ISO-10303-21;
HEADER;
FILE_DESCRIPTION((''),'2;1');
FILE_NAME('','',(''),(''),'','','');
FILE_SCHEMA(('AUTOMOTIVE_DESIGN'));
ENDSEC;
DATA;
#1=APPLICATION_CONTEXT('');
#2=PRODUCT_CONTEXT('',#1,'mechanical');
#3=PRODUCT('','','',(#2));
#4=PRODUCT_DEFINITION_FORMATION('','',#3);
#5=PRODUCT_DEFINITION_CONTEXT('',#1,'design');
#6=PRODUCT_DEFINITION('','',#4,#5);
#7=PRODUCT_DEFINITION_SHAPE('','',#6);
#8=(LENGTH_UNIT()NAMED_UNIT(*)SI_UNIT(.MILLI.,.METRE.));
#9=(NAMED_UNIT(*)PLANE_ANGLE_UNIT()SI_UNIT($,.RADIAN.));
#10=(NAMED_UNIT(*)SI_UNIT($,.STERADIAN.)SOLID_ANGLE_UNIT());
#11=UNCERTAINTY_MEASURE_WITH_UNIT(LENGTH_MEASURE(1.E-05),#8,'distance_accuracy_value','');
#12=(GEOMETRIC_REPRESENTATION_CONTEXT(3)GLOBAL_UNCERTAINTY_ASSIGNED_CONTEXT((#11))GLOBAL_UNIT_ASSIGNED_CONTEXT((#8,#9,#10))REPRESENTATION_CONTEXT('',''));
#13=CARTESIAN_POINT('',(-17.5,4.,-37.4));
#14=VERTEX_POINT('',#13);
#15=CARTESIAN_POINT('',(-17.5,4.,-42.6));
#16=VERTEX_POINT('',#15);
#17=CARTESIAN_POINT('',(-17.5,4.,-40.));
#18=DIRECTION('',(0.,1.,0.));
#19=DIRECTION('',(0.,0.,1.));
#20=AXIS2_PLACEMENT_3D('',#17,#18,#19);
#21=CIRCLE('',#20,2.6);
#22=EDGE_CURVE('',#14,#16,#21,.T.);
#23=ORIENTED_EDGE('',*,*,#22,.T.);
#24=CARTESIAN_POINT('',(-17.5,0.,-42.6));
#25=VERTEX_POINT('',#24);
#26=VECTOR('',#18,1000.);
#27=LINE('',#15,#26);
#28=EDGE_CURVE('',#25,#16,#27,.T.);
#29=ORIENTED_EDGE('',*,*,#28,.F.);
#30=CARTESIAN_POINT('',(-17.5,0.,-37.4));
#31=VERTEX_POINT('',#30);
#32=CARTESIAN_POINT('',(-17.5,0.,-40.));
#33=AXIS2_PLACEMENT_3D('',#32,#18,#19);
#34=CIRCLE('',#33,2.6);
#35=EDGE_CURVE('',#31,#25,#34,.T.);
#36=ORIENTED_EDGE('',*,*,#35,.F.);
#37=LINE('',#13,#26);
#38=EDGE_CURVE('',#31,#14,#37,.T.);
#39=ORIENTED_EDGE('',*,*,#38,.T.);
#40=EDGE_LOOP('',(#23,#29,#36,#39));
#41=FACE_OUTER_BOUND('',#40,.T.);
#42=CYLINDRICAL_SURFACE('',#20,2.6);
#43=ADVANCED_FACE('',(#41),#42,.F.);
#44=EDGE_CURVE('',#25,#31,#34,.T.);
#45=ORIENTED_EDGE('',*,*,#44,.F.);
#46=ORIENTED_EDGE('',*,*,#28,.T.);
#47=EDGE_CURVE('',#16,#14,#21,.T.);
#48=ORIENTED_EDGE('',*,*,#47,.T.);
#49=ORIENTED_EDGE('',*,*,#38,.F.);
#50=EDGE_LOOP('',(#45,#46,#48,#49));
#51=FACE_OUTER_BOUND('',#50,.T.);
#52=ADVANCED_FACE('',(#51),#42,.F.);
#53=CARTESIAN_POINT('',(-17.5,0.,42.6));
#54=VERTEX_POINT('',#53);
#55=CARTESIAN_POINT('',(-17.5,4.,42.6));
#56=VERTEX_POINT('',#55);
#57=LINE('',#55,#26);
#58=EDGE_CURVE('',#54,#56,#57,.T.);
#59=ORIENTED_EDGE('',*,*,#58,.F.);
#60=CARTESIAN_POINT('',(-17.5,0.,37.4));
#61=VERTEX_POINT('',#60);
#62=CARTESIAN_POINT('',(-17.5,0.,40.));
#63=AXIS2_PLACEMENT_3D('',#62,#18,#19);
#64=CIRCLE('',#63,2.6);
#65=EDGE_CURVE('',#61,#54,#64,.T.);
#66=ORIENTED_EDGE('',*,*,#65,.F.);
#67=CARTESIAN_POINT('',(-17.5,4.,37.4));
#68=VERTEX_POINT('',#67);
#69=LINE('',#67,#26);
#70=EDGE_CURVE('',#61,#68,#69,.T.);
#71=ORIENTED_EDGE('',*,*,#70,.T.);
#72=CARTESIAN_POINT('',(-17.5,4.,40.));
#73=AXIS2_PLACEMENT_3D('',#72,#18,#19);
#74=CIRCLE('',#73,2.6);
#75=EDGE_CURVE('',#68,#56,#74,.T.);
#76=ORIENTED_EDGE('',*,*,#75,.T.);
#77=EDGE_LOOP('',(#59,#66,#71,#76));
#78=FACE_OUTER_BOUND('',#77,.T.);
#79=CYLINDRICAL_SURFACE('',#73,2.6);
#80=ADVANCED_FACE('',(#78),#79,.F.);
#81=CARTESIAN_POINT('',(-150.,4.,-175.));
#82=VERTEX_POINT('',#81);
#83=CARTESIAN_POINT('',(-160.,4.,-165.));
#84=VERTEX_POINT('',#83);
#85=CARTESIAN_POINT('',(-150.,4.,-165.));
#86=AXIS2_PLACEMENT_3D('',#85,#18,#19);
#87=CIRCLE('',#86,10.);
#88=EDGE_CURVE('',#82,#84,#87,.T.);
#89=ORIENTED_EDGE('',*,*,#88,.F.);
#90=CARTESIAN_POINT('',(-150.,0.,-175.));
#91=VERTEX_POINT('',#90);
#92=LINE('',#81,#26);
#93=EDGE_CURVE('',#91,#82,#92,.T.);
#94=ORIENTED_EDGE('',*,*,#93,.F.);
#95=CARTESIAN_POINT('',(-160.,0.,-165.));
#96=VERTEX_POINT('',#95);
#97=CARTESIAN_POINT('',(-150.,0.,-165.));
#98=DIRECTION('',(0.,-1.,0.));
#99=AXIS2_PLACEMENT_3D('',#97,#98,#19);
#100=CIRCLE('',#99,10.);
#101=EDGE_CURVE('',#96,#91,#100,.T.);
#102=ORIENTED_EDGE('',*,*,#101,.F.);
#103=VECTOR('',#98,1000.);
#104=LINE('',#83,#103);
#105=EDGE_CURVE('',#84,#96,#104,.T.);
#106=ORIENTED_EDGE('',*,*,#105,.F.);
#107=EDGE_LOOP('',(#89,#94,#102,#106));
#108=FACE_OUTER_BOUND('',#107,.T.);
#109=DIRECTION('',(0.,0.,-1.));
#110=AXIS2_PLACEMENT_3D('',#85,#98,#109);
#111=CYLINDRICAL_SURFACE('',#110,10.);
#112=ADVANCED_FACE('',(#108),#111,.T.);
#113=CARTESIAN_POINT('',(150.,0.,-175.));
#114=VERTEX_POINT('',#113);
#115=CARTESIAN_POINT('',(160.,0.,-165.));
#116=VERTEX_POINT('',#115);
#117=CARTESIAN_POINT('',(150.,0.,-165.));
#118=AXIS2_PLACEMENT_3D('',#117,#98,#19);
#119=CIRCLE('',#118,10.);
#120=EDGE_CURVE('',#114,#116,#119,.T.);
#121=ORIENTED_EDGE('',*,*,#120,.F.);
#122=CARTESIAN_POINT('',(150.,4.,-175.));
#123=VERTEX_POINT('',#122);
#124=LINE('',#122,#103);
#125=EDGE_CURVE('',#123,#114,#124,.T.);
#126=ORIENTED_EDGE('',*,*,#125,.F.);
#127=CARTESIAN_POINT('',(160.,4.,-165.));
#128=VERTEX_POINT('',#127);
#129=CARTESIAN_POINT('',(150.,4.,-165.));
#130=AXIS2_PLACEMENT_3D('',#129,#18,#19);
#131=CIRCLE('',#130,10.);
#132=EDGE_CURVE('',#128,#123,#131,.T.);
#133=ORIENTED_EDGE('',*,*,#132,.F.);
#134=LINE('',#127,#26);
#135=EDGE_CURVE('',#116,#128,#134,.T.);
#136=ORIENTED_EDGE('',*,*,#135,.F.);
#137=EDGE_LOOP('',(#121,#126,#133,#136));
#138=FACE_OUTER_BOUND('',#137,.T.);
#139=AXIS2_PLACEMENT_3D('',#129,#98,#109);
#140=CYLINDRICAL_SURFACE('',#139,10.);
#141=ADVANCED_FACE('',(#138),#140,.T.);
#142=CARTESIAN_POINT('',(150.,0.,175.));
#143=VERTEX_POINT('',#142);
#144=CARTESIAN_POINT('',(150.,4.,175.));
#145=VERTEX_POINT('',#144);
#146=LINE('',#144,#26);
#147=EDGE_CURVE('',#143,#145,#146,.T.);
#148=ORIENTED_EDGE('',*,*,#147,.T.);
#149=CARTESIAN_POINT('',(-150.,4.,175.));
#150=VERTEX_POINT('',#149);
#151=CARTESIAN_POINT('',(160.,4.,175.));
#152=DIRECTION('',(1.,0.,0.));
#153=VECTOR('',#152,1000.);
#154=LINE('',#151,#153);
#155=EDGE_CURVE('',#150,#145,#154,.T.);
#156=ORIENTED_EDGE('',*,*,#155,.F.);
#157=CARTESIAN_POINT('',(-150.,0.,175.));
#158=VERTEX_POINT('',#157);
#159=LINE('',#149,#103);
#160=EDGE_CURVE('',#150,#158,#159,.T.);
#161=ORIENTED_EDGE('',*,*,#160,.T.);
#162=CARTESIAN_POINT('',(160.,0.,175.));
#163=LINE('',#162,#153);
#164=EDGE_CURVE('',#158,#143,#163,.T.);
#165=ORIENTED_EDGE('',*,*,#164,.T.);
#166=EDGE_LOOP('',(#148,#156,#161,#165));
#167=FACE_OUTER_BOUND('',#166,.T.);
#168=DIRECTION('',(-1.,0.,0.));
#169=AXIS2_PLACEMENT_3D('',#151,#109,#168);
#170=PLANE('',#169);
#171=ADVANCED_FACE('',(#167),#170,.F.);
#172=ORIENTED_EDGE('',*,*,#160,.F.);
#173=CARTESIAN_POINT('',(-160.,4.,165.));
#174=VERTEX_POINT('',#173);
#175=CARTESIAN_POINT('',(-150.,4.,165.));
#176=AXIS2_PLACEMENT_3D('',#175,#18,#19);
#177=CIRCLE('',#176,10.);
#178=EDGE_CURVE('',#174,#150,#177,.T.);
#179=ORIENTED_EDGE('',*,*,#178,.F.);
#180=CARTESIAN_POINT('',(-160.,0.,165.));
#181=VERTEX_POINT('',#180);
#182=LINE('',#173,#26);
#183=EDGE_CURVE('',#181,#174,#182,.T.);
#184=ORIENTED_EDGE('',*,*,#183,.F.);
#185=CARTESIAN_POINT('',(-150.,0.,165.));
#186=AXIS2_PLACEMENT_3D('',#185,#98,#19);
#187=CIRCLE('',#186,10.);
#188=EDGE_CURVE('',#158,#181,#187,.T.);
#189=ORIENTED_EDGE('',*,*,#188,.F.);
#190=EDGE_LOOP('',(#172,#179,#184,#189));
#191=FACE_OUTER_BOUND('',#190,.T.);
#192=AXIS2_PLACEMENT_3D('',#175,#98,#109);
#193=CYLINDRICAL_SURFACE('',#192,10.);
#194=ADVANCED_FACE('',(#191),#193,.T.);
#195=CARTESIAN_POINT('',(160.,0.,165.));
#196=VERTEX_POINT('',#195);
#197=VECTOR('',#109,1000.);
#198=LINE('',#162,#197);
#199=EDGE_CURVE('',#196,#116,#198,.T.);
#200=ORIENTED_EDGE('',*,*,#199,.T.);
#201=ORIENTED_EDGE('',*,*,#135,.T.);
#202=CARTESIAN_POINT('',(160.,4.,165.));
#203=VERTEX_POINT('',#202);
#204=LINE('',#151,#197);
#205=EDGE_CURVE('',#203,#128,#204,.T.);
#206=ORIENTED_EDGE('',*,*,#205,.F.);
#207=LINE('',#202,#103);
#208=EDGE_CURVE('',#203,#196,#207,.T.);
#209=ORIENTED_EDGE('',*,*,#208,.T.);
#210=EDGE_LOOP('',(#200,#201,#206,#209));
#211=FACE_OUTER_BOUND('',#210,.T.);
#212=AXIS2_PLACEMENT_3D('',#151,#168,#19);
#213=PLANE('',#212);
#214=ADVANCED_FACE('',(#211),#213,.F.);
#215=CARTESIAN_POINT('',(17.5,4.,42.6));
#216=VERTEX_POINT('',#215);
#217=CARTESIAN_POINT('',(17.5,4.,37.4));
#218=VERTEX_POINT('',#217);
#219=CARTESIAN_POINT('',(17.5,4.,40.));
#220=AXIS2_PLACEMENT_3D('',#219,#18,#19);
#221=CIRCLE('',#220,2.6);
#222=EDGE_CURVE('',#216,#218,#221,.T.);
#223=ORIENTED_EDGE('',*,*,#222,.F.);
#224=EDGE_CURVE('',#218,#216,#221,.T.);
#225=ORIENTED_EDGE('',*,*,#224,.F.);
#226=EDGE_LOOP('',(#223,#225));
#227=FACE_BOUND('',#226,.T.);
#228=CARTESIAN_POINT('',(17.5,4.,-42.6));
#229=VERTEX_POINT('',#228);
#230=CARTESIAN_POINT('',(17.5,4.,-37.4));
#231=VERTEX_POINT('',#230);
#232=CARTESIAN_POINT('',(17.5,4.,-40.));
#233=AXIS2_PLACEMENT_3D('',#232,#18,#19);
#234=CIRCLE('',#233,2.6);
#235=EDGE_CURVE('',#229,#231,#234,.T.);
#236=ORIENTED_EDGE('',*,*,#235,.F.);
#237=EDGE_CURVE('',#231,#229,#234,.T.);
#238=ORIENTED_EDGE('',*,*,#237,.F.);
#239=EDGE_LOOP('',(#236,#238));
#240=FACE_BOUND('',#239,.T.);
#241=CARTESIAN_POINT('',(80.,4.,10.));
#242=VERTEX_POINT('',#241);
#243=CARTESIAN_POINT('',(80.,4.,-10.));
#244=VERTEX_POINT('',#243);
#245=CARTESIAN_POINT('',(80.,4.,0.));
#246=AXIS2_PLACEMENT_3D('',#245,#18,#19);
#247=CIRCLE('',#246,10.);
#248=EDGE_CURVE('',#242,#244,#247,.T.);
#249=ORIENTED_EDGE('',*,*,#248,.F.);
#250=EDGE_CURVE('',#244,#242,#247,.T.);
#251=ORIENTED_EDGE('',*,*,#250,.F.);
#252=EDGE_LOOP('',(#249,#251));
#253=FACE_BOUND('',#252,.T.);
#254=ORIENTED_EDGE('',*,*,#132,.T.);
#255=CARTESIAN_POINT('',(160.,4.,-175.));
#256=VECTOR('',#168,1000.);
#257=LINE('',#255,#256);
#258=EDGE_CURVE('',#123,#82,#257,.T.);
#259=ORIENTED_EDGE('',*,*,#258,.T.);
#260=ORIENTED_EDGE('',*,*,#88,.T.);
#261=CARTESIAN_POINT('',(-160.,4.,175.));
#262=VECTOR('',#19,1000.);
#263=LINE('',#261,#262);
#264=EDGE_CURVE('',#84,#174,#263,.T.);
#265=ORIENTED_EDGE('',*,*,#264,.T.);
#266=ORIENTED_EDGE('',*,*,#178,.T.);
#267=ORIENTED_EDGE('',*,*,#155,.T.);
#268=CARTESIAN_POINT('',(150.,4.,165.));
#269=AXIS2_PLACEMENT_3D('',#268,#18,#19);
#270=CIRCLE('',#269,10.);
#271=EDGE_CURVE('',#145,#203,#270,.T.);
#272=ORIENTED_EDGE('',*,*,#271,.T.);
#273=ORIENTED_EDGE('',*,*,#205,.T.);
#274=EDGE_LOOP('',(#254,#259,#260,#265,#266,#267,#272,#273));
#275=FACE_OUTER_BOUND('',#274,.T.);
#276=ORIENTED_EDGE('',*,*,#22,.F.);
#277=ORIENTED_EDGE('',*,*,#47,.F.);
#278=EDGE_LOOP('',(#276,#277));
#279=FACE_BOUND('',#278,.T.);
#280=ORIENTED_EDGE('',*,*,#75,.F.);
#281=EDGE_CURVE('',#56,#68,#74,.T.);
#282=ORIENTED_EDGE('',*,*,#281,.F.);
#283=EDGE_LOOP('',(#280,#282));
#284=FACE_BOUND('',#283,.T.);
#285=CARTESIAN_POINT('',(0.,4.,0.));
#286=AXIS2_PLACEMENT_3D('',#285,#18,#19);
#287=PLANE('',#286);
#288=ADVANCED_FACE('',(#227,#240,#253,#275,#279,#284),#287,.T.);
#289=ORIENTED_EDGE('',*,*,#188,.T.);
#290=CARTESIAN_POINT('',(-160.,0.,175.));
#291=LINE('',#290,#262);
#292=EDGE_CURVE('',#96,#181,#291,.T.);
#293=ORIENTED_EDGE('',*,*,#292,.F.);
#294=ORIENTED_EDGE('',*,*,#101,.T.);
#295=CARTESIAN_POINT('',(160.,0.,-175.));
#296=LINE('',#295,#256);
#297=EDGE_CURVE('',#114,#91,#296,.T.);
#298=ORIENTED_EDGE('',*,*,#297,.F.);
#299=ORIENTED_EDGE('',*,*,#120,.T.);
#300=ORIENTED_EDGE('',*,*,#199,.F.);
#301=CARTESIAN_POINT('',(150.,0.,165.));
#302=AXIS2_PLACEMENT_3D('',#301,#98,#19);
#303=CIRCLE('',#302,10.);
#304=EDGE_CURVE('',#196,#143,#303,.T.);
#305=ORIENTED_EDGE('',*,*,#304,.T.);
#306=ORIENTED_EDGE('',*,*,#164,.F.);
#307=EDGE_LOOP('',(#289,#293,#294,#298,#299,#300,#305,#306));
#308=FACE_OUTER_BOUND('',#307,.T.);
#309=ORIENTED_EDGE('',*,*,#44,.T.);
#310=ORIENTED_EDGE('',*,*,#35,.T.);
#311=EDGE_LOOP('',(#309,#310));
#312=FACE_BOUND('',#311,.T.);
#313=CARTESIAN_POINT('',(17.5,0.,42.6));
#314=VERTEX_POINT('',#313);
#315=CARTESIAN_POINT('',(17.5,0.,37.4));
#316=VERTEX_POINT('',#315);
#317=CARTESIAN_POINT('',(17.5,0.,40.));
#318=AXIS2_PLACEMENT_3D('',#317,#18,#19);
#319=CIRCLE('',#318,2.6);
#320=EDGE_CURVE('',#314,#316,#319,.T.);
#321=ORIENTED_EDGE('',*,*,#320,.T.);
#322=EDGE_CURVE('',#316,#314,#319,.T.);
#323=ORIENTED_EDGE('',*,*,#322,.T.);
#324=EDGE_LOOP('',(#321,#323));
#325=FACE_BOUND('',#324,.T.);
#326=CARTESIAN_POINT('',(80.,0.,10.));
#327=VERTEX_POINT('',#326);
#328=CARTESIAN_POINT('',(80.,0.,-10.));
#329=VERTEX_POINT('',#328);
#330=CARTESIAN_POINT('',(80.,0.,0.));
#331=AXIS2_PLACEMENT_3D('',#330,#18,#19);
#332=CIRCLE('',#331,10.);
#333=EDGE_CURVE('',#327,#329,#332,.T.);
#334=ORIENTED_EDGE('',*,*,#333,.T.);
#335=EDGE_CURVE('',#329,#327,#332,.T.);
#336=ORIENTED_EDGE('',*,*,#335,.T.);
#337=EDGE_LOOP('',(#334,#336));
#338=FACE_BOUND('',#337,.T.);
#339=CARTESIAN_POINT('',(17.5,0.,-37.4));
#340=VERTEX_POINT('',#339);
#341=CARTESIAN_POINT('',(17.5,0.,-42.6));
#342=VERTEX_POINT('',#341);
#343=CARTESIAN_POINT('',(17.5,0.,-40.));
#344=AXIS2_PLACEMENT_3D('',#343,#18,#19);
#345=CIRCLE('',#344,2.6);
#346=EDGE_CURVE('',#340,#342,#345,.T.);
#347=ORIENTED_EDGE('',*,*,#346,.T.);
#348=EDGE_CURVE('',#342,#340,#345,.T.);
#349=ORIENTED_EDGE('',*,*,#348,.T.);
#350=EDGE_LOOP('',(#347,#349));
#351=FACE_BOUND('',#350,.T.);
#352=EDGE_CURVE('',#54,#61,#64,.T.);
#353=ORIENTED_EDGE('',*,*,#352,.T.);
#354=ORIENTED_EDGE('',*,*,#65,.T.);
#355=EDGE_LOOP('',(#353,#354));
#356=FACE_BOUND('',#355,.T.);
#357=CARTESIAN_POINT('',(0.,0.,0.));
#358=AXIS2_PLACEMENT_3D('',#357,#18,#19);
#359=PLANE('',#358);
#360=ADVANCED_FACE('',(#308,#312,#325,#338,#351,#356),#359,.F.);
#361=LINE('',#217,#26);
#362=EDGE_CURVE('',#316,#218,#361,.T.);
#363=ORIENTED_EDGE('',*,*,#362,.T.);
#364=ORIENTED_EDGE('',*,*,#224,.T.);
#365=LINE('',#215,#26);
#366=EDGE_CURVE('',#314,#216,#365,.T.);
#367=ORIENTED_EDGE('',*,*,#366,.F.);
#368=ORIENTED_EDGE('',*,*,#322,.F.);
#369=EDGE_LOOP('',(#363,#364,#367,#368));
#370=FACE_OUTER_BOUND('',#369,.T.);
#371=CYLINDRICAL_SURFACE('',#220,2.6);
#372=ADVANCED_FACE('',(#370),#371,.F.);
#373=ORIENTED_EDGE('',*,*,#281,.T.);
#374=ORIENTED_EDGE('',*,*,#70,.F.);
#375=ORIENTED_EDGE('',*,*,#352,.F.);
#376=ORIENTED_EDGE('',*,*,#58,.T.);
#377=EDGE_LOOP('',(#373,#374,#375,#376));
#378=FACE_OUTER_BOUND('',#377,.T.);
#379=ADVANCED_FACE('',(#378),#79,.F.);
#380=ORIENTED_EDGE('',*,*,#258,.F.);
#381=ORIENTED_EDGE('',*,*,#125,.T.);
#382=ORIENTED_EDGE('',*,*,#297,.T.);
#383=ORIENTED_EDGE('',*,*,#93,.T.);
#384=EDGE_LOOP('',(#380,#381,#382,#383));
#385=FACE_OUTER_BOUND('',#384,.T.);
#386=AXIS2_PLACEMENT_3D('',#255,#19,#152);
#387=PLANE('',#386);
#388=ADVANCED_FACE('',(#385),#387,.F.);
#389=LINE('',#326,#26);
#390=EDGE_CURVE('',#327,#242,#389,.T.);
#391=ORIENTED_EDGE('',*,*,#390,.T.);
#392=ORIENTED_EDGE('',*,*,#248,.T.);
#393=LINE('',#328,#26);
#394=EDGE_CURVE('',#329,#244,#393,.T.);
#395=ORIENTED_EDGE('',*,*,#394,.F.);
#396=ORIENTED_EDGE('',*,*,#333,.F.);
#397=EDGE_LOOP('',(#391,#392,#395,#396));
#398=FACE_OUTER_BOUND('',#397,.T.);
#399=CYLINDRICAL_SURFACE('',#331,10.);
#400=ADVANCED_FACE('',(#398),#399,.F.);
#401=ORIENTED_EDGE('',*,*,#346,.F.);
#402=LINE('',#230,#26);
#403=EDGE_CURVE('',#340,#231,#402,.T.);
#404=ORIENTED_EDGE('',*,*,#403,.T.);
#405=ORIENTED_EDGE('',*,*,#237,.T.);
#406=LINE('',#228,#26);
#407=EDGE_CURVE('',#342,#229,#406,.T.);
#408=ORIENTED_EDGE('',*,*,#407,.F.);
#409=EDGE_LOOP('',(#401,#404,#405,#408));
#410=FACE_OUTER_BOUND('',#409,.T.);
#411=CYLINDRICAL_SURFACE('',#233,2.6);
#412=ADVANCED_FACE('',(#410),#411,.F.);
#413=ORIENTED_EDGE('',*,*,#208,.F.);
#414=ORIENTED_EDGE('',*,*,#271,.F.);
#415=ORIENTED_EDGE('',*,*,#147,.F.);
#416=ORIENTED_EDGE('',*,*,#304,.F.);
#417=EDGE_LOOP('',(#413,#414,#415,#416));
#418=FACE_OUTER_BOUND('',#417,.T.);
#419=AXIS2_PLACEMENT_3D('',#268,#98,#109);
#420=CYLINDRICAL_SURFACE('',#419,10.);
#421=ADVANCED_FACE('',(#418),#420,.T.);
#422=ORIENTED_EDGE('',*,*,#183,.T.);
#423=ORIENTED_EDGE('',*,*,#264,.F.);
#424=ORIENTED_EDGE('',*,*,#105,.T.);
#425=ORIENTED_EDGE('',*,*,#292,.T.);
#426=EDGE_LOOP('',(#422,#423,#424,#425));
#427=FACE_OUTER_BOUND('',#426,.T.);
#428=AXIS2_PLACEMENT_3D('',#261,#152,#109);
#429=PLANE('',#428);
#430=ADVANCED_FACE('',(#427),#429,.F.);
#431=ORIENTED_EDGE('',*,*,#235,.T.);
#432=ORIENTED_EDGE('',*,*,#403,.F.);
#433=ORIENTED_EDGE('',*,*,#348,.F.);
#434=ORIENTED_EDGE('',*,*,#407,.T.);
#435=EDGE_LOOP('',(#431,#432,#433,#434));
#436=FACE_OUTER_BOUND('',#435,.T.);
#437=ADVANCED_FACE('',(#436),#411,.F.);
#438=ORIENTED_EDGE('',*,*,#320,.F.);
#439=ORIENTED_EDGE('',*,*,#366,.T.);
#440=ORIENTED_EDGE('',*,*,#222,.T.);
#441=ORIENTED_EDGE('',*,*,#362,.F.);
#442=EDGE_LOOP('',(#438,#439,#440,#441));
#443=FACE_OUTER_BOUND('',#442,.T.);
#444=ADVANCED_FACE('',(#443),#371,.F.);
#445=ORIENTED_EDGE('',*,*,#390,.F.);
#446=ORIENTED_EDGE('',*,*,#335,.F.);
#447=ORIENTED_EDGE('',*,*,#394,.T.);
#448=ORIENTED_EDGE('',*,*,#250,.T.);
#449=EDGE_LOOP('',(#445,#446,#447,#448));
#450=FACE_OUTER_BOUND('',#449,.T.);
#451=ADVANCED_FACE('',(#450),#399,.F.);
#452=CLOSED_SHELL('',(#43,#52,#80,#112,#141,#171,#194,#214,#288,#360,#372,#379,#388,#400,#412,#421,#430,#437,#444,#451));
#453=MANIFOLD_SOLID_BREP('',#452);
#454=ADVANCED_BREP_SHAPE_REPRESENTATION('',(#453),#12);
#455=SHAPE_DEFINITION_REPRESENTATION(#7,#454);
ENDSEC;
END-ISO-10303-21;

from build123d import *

# Parameters (mm, degrees)
SKETCH1_W                      = 320
SKETCH1_H                      = 350
BOSS_EXTRUDE1_DEPTH            = 4
F_5_2_5_2_DIAMETER_HOLE1_D     = 5.2
F_5_2_5_2_DIAMETER_HOLE1_DEPTH = 10.1
F_5_2_5_2_DIAMETER_HOLE1_TIP   = 1.562237609
FILLET1_R                      = 10
SKETCH4_R                      = 10
CUT_EXTRUDE1_DEPTH             = 238.151850088


with BuildPart() as part:
    # Sketch1 → Boss-Extrude1 (new body)
    with BuildSketch(Plane(origin=(0, 0, 0), x_dir=(1, 0, 0), z_dir=(0, 1, 0))):
        Rectangle(SKETCH1_W, SKETCH1_H)
    extrude(amount=BOSS_EXTRUDE1_DEPTH)

    # Ø5.2 (5.2) Diameter Hole1
    with Locations(Plane(origin=(0, 4, 0), x_dir=(1, 0, 0), z_dir=(0, 1, 0))):
        with Locations((-17.5, 40), (17.5, -40), (-17.5, -40), (17.5, 40)):
            Hole(F_5_2_5_2_DIAMETER_HOLE1_D / 2, depth=F_5_2_5_2_DIAMETER_HOLE1_DEPTH)
            with Locations((0, 0, -(F_5_2_5_2_DIAMETER_HOLE1_DEPTH + F_5_2_5_2_DIAMETER_HOLE1_TIP / 2))):  # 118° drill point
                Cone(0, F_5_2_5_2_DIAMETER_HOLE1_D / 2, F_5_2_5_2_DIAMETER_HOLE1_TIP, mode=Mode.SUBTRACT)

    # Fillet1
    fillet1_edges = [part.edges().sort_by_distance(p)[0] for p in [
        (-160, 2, -175),
        (160, 2, -175),
        (160, 2, 175),
        (-160, 2, 175),
    ]]
    fillet(fillet1_edges, radius=FILLET1_R)

    # Sketch4 → Cut-Extrude1 (cut, through all)
    with BuildSketch(Plane(origin=(0, 4, 0), x_dir=(1, 0, 0), z_dir=(0, 1, 0))):
        with Locations(Location((80, 0, 0), (0, 0, 270))):
            Circle(SKETCH4_R)
    extrude(amount=-CUT_EXTRUDE1_DEPTH, mode=Mode.SUBTRACT)


solid = part.part
